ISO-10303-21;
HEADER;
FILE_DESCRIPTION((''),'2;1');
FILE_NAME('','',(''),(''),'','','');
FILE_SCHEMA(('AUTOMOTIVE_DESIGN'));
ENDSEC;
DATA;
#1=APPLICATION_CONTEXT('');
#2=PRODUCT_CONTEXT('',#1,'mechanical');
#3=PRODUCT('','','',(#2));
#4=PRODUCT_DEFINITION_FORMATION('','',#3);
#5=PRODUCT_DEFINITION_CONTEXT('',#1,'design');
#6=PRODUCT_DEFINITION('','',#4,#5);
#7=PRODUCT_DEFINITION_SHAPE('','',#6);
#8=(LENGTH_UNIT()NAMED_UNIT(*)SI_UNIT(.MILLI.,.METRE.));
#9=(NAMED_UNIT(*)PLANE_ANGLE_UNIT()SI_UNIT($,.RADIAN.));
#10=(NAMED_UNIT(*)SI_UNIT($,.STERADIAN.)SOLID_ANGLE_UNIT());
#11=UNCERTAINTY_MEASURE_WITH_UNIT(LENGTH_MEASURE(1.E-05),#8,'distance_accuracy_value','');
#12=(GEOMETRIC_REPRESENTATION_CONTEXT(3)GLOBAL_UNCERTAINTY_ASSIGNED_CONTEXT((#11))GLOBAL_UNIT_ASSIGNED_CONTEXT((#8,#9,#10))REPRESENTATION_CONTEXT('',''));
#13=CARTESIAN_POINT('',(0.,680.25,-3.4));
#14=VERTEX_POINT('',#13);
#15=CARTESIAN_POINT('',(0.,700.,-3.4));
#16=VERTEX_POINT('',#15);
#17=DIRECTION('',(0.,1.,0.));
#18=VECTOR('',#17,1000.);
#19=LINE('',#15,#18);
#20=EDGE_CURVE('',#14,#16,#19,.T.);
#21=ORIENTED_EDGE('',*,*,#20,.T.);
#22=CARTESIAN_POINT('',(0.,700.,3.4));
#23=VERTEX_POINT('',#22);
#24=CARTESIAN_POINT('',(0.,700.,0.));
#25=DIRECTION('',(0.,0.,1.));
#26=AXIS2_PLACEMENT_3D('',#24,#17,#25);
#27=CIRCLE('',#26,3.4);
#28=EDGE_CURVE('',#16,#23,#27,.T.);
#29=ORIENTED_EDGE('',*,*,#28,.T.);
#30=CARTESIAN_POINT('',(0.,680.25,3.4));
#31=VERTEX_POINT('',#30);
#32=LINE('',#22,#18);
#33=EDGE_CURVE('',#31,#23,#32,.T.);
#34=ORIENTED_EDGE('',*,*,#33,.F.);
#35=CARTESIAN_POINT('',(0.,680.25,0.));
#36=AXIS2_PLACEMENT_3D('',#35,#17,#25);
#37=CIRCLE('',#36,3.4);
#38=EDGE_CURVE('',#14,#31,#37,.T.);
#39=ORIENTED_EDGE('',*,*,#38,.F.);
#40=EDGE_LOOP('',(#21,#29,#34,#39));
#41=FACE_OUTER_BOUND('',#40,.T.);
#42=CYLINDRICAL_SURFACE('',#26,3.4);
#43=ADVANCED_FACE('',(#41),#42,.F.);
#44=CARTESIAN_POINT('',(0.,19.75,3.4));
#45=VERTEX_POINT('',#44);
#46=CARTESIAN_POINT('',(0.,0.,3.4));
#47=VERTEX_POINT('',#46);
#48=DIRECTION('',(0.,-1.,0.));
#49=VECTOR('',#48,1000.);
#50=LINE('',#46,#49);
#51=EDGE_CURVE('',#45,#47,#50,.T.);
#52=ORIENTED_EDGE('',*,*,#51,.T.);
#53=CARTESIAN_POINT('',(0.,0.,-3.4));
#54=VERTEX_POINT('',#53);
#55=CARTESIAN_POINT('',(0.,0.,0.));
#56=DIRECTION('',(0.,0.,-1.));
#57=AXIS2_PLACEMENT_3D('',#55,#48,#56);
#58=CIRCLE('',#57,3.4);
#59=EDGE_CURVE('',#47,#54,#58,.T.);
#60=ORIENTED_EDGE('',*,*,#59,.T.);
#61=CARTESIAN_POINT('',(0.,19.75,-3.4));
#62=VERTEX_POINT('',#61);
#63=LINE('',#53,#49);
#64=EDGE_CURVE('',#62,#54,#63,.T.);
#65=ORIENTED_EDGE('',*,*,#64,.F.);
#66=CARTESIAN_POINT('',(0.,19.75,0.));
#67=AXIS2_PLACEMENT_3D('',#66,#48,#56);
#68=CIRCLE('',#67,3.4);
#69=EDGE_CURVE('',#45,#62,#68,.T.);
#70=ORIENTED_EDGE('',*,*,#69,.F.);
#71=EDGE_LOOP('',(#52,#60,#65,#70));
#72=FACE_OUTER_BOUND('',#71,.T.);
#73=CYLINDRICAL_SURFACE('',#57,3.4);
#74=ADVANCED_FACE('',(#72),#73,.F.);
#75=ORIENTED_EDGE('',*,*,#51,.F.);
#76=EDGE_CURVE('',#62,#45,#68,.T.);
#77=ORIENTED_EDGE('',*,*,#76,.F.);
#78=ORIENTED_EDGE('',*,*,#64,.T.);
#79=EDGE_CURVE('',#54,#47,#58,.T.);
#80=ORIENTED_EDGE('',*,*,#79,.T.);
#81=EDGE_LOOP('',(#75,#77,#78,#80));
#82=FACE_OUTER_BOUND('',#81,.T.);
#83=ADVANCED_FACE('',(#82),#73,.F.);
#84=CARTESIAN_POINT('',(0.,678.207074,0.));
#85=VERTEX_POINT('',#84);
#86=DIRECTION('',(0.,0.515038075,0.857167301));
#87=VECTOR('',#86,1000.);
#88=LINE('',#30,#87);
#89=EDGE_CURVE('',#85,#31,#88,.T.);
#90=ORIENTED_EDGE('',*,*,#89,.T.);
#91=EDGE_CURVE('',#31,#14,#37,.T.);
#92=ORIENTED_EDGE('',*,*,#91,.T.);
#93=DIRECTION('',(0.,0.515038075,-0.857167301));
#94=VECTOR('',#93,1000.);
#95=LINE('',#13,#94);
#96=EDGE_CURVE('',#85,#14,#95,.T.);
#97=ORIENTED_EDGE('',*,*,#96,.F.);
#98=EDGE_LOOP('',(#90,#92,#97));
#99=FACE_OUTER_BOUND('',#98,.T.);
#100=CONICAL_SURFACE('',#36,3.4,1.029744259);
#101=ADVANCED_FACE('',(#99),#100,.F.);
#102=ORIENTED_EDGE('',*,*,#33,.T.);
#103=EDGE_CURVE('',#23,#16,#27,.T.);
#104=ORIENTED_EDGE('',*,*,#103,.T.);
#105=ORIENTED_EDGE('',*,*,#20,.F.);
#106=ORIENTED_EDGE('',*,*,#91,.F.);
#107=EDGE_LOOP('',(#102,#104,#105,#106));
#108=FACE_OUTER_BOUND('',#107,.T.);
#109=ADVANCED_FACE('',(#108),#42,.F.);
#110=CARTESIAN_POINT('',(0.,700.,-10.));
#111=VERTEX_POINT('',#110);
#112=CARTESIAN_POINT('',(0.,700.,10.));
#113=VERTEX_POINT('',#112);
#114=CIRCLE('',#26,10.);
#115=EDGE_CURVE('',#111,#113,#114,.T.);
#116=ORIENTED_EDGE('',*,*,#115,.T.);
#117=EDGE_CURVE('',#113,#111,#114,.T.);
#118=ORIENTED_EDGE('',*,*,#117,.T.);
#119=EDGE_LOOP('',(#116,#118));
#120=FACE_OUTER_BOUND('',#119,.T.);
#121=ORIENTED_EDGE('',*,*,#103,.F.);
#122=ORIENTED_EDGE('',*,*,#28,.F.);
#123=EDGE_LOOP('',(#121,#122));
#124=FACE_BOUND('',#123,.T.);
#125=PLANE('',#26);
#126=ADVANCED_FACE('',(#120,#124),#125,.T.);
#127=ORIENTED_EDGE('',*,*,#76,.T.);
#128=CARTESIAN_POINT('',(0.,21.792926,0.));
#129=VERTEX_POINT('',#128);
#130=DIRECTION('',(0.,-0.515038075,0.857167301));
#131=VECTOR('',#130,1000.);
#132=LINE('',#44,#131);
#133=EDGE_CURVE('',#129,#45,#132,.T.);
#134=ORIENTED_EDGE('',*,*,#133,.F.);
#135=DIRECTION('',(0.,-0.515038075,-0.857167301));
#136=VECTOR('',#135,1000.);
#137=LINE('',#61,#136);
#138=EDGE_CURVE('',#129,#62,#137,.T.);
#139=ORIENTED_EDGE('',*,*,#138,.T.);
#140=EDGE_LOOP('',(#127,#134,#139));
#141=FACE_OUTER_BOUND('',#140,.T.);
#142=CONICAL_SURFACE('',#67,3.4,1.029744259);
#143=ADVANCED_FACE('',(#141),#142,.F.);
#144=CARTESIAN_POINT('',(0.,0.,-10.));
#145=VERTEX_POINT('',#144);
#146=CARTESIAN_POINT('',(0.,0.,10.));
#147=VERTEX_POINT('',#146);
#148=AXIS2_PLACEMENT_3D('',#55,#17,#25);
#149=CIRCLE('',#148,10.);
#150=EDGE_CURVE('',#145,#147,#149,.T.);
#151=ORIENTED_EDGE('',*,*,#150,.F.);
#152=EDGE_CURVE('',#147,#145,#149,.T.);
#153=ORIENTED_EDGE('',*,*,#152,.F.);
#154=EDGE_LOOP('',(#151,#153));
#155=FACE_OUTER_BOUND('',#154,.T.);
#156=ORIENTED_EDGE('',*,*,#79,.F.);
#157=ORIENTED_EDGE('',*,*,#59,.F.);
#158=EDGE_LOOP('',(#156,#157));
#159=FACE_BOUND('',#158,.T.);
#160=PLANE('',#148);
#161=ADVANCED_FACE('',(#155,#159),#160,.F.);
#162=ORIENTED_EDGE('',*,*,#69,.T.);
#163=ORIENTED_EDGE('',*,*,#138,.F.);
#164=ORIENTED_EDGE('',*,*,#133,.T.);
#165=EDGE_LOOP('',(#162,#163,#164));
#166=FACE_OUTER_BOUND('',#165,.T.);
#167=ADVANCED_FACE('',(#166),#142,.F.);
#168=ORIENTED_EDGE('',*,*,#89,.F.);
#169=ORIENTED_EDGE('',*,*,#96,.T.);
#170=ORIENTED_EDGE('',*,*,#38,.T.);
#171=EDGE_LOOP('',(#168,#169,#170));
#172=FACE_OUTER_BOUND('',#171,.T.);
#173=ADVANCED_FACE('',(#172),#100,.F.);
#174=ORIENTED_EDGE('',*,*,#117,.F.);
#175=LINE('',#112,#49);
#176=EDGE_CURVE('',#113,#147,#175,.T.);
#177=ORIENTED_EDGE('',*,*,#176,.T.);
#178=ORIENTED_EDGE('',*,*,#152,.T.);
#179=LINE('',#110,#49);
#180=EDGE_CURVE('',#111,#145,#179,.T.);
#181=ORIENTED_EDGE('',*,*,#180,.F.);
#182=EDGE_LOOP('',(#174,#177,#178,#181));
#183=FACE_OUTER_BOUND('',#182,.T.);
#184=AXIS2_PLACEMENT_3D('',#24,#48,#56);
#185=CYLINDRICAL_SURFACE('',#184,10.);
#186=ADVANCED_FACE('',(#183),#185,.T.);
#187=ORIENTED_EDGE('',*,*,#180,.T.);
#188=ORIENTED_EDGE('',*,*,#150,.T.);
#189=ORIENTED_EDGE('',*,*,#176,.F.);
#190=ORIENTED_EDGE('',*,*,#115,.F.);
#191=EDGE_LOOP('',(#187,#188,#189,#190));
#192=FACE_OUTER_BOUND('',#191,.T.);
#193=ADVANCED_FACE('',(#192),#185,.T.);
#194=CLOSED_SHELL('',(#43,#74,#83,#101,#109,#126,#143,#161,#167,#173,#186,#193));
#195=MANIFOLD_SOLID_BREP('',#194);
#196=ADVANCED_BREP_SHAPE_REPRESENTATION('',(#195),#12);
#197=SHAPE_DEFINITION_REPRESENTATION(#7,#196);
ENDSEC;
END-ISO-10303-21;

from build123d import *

# Parameters (mm, degrees)
SKETCH1_R             = 10
BOSS_EXTRUDE1_DEPTH   = 700
M8_TAPPED_HOLE1_D     = 6.8
M8_TAPPED_HOLE1_DEPTH = 19.75
M8_TAPPED_HOLE1_TIP   = 2.042926105
M8_TAPPED_HOLE2_D     = 6.8
M8_TAPPED_HOLE2_DEPTH = 19.75
M8_TAPPED_HOLE2_TIP   = 2.042926105


with BuildPart() as part:
    # Sketch1 → Boss-Extrude1 (new body)
    with BuildSketch(Plane(origin=(0, 0, 0), x_dir=(1, 0, 0), z_dir=(0, 1, 0))):
        with Locations(Location((0, 0, 0), (0, 0, 270))):
            Circle(SKETCH1_R)
    extrude(amount=BOSS_EXTRUDE1_DEPTH)

    # M8 Tapped Hole1
    with Locations(Plane(origin=(0, 700, 0), x_dir=(1, 0, 0), z_dir=(0, 1, 0))):
        with Locations((0, 0)):
            Hole(M8_TAPPED_HOLE1_D / 2, depth=M8_TAPPED_HOLE1_DEPTH)
            with Locations((0, 0, -(M8_TAPPED_HOLE1_DEPTH + M8_TAPPED_HOLE1_TIP / 2))):  # 118° drill point
                Cone(0, M8_TAPPED_HOLE1_D / 2, M8_TAPPED_HOLE1_TIP, mode=Mode.SUBTRACT)

    # M8 Tapped Hole2
    with Locations(Plane(origin=(0, 0, 0), x_dir=(-1, 0, 0), z_dir=(0, -1, 0))):
        with Locations((0, 0)):
            Hole(M8_TAPPED_HOLE2_D / 2, depth=M8_TAPPED_HOLE2_DEPTH)
            with Locations((0, 0, -(M8_TAPPED_HOLE2_DEPTH + M8_TAPPED_HOLE2_TIP / 2))):  # 118° drill point
                Cone(0, M8_TAPPED_HOLE2_D / 2, M8_TAPPED_HOLE2_TIP, mode=Mode.SUBTRACT)


solid = part.part
